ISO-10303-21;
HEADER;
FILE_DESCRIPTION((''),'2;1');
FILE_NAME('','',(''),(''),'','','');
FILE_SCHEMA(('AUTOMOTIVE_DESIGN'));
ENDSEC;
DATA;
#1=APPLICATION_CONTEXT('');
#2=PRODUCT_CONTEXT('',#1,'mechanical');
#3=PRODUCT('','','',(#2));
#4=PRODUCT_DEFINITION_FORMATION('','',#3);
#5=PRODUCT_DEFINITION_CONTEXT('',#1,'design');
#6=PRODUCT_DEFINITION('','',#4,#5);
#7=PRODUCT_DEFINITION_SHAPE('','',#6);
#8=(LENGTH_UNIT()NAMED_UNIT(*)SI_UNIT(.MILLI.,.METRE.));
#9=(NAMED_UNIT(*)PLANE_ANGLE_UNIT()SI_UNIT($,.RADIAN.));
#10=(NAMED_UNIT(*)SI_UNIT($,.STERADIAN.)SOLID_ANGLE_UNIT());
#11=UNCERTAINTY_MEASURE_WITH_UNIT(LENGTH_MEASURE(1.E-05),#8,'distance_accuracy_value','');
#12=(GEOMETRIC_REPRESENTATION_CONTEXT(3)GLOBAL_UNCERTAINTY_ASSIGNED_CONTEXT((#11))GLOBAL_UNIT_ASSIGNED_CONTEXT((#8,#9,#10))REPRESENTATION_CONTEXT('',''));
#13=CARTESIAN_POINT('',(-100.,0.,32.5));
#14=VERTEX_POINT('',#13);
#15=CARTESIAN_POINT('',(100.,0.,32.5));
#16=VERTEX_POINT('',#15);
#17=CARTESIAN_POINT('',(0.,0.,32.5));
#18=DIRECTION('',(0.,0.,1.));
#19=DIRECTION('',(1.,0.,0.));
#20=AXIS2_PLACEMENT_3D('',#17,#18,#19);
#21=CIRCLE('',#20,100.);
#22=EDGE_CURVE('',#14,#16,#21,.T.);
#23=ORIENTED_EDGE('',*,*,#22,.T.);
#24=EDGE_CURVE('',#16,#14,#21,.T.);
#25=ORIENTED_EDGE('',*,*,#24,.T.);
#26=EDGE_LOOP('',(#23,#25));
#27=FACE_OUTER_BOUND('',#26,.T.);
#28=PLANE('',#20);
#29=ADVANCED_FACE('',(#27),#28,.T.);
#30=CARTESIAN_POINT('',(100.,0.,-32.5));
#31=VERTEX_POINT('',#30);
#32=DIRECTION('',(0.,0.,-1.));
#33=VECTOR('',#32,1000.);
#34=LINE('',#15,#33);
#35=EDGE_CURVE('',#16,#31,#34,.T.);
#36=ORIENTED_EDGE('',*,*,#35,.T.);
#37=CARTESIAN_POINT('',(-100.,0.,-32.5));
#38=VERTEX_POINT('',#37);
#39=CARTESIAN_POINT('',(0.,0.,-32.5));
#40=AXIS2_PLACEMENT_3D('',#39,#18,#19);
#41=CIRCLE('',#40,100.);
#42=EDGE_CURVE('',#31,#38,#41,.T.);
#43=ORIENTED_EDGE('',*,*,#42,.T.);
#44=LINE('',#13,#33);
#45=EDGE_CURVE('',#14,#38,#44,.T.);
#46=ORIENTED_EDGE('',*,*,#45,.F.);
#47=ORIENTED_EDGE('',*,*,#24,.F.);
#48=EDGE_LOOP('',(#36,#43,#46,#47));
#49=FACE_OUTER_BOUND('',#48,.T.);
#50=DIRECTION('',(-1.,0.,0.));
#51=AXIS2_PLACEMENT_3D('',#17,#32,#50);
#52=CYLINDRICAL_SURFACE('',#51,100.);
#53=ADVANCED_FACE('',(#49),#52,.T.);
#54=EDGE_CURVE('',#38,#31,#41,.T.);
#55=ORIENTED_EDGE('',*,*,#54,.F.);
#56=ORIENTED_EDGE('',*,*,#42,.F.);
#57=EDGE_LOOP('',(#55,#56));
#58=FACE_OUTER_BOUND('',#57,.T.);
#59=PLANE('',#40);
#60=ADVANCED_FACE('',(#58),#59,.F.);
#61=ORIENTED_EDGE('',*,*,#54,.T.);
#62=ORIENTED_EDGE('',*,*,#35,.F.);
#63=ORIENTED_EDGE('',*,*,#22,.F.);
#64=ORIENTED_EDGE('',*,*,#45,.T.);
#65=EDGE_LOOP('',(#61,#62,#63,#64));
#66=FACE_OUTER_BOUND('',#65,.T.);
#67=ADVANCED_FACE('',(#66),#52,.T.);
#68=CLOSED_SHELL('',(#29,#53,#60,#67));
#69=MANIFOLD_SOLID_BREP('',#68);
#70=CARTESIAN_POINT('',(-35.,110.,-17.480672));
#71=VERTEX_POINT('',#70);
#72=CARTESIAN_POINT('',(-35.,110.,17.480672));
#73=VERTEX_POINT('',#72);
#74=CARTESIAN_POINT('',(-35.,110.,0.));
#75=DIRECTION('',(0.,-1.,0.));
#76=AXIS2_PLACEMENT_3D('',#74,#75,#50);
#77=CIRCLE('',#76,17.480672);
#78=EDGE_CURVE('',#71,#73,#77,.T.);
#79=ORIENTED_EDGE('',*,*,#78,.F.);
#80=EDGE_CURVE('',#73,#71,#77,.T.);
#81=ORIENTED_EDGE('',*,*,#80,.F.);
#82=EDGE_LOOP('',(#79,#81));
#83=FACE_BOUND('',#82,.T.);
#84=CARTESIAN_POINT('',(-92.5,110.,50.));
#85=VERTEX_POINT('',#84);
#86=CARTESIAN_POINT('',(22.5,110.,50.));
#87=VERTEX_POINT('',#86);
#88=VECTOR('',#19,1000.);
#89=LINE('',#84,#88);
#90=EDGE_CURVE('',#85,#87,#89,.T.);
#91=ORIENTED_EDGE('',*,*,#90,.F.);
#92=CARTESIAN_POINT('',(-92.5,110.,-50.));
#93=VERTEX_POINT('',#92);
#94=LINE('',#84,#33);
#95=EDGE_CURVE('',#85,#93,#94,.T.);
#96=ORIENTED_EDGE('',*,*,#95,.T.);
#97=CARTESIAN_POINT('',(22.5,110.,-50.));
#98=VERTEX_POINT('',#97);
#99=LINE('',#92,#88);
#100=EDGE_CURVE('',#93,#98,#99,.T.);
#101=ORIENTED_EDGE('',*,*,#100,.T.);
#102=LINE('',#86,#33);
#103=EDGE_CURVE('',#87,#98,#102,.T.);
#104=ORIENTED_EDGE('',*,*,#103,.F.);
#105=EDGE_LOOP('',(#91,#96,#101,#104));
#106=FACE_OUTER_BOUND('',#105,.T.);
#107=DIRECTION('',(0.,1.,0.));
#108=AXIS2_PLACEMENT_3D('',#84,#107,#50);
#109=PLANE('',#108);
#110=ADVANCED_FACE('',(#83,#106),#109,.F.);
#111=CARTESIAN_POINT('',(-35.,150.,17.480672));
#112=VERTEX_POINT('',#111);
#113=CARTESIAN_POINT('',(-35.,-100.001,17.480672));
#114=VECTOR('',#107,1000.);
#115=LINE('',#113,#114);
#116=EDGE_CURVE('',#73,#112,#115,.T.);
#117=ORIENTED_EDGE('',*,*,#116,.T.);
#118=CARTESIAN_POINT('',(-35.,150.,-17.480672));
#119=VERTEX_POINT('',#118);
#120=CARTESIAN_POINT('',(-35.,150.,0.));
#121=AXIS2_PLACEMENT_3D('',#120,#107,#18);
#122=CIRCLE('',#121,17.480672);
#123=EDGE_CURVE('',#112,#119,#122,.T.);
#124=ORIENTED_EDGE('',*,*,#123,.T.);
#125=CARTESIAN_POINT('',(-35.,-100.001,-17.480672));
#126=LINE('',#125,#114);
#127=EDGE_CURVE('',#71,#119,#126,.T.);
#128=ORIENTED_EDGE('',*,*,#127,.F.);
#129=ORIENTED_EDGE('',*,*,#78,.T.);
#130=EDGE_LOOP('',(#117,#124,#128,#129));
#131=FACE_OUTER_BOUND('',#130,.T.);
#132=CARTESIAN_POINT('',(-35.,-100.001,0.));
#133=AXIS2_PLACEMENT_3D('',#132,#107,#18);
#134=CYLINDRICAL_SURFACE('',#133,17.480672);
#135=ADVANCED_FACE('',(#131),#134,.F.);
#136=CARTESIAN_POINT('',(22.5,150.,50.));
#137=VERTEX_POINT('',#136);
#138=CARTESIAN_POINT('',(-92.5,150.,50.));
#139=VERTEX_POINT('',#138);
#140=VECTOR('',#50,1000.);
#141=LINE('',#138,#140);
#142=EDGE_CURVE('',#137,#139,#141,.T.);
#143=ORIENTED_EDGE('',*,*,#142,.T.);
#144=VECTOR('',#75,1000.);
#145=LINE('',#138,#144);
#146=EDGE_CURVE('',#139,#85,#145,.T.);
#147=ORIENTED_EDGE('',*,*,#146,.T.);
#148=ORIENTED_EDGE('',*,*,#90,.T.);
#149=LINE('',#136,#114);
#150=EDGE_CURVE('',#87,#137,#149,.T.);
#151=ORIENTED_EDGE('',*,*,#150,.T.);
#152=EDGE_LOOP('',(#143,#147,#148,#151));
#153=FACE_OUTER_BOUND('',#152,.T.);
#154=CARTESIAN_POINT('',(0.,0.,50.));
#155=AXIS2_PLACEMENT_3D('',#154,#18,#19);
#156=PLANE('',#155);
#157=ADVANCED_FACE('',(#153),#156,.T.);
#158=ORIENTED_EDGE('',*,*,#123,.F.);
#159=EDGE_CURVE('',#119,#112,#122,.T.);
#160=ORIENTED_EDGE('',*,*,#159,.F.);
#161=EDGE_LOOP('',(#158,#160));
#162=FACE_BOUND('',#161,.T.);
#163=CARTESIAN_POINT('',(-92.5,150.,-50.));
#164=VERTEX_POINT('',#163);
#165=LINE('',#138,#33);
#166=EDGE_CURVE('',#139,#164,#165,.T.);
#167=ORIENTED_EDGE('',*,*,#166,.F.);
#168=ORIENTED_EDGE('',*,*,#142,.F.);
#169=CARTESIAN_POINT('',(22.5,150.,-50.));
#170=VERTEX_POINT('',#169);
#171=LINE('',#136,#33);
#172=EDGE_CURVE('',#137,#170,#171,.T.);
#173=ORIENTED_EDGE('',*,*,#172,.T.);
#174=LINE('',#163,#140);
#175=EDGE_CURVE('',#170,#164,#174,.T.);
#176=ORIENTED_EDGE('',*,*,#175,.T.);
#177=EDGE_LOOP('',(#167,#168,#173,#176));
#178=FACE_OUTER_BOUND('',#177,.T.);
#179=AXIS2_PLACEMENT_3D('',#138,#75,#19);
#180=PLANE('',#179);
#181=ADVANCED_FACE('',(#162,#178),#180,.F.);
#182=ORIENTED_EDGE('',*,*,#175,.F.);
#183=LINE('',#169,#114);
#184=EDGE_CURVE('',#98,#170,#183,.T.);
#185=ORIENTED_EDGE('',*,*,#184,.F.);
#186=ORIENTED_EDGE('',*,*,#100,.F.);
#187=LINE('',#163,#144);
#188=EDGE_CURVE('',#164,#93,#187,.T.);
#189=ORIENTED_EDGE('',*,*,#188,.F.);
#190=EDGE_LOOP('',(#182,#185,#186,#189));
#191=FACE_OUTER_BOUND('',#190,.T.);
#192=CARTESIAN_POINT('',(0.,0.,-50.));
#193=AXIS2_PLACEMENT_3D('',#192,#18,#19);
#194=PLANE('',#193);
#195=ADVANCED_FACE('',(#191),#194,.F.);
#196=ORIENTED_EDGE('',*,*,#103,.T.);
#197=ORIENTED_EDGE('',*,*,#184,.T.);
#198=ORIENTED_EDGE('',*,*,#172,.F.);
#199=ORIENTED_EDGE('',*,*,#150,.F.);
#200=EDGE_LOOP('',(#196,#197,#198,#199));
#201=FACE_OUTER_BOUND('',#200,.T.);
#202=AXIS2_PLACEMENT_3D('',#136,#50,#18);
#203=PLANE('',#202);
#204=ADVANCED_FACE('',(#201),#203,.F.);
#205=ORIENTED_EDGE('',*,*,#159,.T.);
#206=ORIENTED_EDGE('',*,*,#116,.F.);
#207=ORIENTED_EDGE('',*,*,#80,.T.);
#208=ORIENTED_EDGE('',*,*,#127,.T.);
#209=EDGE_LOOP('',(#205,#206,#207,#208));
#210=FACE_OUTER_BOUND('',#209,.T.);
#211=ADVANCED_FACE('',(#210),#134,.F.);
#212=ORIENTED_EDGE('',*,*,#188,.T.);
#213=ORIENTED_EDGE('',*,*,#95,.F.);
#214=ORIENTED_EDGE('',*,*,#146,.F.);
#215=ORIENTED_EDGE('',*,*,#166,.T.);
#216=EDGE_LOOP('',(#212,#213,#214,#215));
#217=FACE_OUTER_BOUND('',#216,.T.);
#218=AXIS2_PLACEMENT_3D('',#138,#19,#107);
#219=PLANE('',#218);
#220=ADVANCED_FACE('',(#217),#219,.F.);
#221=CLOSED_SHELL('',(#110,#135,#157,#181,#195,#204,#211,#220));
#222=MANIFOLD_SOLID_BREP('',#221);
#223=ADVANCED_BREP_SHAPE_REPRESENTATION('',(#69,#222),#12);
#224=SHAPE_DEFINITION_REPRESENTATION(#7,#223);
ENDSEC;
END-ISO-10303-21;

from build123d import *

# Parameters (mm, degrees)
SKETCH_1_R          = 100
EXTRUDE_1_DEPTH     = 32.5
SKETCH_2_W          = 115
SKETCH_2_H          = 40
EXTRUDE_2_DEPTH     = 50
SKETCH_3_R          = 17.480672493
CUT_EXTRUDE_1_DEPTH = 40


with BuildPart() as part:
    # 草图1 → 凸台-拉伸1 (new, symmetric)
    with BuildSketch(Plane.XY):
        Circle(SKETCH_1_R)
    extrude(amount=EXTRUDE_1_DEPTH, both=True)


with BuildPart() as body_2:
    # 草图2 → 凸台-拉伸2 (new, symmetric)
    with BuildSketch(Plane.XY):
        with Locations((-35, 130)):
            Rectangle(SKETCH_2_W, SKETCH_2_H)
    extrude(amount=EXTRUDE_2_DEPTH, both=True)

    # 草图3 → 切除-拉伸1 (cut)
    with BuildSketch(Plane(origin=(0, 150, 0), x_dir=(1, 0, 0), z_dir=(0, 1, 0))):
        with Locations(Location((-35, 0, 0), (0, 0, 270))):
            Circle(SKETCH_3_R)
    extrude(amount=-CUT_EXTRUDE_1_DEPTH, mode=Mode.SUBTRACT)


solid = Compound([part.part, body_2.part])
